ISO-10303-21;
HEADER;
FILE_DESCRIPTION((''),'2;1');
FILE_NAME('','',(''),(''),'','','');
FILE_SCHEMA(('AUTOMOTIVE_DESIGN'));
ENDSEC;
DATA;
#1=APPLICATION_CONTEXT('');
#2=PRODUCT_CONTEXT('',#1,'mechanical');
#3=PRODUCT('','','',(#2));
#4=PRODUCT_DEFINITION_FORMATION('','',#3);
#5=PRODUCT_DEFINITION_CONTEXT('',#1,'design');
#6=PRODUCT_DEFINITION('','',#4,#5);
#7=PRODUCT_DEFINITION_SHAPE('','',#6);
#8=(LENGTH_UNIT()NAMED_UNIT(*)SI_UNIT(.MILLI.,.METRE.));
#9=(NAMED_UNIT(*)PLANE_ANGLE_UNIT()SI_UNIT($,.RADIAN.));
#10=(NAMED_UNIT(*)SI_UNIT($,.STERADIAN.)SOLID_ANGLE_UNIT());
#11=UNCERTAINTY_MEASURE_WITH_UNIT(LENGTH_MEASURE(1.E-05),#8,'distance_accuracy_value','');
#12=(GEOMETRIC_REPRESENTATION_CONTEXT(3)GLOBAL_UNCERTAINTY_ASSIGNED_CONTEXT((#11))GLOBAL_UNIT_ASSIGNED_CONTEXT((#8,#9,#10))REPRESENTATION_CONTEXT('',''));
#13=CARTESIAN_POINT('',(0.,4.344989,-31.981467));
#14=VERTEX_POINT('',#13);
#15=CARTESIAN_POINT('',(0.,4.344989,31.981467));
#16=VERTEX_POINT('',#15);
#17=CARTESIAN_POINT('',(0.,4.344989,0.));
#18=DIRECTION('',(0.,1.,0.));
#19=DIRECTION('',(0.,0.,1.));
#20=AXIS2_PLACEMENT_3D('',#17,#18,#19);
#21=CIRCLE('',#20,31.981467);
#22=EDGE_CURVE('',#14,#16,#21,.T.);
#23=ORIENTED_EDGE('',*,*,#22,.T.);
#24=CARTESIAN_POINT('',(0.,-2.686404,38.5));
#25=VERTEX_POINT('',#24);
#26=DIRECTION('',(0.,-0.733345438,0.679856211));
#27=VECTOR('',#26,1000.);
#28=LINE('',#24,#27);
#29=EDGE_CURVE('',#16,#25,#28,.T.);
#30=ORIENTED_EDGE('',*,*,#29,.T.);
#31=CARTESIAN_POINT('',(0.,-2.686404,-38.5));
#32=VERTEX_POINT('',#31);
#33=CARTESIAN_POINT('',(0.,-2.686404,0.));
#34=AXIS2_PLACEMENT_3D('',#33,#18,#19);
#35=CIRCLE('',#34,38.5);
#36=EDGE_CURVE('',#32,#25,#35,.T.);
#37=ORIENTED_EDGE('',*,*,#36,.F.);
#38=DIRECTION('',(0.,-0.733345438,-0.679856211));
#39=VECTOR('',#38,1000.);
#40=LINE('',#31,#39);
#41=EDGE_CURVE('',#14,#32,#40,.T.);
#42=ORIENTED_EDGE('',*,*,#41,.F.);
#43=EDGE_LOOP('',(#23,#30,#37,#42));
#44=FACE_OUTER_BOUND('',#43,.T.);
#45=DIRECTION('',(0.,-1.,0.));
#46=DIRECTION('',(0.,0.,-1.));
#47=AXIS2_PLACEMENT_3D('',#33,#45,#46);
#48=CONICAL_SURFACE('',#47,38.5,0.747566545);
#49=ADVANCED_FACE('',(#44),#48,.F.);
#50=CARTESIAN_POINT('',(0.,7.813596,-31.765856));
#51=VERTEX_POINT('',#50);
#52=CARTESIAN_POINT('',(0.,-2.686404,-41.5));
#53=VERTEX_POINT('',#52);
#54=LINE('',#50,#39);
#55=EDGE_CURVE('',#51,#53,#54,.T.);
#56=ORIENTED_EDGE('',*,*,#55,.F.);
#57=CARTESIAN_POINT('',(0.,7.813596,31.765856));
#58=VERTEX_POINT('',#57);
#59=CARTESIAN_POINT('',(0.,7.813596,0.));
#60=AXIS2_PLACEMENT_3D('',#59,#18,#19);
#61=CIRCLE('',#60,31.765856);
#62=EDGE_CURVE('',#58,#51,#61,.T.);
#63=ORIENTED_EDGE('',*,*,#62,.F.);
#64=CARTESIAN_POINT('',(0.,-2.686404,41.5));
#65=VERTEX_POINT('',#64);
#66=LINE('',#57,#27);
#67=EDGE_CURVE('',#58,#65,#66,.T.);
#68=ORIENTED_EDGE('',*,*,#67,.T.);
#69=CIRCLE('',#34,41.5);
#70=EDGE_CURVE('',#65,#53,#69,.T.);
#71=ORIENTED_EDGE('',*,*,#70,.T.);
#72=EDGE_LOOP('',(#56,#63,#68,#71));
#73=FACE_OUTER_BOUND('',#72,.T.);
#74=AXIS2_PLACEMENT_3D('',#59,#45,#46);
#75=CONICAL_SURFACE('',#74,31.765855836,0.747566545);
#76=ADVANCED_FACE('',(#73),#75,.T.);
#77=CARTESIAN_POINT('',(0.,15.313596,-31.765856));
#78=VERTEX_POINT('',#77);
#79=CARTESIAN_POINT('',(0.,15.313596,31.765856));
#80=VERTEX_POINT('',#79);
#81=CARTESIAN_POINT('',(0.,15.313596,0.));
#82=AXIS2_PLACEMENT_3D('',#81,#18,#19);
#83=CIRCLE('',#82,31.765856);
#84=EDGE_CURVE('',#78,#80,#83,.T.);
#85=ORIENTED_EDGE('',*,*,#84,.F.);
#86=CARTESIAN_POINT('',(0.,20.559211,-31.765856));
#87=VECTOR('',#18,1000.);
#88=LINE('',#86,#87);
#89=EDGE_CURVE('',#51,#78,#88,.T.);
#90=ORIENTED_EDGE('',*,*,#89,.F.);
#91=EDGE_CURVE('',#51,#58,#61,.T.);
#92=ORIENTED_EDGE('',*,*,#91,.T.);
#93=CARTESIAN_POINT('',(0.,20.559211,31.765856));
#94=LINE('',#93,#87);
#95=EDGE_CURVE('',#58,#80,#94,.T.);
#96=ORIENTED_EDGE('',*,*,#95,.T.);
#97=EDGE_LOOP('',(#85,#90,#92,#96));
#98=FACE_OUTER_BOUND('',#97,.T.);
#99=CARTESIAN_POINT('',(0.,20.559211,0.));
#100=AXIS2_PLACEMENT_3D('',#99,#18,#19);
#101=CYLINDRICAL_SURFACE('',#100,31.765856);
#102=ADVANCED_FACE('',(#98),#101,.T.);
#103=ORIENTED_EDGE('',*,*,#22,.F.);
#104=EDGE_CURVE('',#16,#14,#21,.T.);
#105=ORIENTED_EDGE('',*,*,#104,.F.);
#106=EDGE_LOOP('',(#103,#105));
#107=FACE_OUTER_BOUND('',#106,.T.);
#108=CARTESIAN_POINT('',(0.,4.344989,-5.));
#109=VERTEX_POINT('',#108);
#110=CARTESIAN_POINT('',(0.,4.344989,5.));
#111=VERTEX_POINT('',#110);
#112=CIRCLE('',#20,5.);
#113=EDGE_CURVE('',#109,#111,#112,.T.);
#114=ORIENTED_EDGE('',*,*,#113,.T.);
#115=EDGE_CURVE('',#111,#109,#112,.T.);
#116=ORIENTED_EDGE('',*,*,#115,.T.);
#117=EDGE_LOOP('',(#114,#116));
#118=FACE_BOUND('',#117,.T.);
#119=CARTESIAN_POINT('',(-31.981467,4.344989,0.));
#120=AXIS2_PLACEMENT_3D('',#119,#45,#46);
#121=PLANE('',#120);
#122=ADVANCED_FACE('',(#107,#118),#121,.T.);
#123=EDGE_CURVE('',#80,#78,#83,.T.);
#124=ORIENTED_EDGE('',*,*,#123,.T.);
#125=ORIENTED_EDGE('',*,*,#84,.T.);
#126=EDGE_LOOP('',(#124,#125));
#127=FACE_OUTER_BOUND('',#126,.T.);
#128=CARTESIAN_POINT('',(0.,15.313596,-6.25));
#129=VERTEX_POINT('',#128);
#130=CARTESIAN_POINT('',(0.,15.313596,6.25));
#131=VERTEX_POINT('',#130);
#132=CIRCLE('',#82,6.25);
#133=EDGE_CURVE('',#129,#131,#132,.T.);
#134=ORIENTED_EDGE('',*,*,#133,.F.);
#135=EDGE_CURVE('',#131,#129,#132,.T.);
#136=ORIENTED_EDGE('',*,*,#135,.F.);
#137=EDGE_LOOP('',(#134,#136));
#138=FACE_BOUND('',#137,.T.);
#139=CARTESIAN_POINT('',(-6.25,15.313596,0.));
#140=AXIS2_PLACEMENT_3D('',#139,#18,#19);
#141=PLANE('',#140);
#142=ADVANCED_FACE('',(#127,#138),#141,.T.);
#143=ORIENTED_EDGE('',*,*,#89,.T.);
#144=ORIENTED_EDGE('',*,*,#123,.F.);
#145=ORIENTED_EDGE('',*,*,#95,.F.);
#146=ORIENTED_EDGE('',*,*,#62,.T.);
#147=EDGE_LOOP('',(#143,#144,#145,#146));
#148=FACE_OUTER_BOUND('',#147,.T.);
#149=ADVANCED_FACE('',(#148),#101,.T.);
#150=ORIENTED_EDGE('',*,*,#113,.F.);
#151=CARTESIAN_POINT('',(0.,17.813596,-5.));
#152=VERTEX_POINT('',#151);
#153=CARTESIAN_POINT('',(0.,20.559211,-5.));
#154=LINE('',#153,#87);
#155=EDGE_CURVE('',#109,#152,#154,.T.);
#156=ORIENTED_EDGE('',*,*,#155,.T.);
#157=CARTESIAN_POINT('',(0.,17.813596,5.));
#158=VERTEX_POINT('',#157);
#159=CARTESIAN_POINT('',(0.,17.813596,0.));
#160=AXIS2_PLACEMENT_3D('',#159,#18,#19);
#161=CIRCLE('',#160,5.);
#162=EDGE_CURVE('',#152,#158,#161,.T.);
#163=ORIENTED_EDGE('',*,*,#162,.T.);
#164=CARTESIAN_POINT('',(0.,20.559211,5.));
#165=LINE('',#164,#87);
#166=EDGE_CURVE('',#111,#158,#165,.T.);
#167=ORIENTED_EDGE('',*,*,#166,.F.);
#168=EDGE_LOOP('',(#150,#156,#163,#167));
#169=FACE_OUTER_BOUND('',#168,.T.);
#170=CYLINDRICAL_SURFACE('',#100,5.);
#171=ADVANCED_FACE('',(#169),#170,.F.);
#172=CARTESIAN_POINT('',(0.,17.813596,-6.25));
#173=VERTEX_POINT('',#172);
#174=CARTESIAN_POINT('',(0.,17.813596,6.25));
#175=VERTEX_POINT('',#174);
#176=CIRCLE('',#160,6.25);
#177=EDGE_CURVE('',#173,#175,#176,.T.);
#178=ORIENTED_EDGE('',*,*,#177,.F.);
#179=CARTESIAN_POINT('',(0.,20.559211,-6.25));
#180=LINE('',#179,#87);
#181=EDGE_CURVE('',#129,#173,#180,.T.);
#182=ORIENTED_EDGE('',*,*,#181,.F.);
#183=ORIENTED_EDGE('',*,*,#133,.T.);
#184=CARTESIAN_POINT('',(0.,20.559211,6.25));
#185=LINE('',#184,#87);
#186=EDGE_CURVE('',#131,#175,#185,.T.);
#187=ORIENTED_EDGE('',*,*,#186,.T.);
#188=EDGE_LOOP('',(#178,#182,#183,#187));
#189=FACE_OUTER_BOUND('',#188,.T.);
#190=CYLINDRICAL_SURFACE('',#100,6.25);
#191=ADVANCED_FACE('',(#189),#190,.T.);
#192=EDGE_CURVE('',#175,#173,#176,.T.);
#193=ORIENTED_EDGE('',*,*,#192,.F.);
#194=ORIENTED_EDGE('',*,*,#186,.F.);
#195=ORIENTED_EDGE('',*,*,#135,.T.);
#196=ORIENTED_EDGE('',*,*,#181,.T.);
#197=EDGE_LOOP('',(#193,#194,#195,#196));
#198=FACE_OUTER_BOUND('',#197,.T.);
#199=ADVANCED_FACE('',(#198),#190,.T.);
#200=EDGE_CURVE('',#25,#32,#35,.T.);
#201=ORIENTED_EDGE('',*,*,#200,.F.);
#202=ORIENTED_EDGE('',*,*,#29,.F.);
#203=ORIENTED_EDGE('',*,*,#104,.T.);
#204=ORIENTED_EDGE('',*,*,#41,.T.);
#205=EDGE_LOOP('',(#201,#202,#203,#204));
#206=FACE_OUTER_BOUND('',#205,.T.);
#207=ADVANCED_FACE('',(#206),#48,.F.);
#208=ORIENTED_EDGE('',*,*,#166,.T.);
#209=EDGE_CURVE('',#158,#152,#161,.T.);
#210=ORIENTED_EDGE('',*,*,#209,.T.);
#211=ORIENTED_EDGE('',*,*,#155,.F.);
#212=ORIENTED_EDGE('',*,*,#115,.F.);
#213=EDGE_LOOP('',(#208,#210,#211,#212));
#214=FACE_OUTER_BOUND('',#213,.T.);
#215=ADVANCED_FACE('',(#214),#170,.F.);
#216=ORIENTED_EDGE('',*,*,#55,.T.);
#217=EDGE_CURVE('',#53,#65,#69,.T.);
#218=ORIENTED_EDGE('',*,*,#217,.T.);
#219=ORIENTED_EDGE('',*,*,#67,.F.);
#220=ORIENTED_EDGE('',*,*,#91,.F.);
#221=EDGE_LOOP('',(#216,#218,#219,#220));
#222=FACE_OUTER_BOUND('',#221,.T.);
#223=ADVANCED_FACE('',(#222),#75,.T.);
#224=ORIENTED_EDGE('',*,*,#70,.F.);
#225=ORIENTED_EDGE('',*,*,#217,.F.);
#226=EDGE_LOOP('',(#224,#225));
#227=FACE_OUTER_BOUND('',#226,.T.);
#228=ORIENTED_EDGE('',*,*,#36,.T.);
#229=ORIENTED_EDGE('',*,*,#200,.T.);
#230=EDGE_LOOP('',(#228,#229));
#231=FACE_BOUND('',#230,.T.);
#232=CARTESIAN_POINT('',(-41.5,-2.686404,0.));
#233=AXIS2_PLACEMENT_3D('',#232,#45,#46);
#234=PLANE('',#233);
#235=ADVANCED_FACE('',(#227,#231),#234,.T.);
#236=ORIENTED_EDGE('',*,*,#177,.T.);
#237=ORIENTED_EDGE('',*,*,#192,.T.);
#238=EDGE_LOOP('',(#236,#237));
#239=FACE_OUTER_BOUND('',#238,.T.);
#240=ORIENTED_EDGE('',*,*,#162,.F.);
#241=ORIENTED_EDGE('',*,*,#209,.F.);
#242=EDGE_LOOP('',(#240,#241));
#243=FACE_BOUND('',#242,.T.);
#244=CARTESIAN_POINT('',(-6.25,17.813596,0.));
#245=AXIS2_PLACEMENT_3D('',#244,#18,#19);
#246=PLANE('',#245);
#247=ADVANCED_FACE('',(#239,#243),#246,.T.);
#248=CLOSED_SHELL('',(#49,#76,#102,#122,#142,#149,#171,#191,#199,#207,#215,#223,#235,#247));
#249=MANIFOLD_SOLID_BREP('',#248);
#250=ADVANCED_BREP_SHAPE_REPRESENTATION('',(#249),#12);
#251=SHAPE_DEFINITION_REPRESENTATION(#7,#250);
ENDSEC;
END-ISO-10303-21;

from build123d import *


with BuildPart() as part:
    # 草图1 → 旋转1 (revolve)
    with BuildSketch(Plane.XY, mode=Mode.PRIVATE) as revolve_1_sk:
        Polygon((-6.25, 17.813596491), (-5, 17.813596491), (-5, 4.34498949), (-31.981467322, 4.34498949), (-38.5, -2.686403509), (-41.5, -2.686403509), (-31.765855836, 7.813596491), (-31.765855836, 15.313596491), (-6.25, 15.313596491), align=None)
    revolve(revolve_1_sk.sketch.rotate(Axis((0, 20.559210526, 0), (0, -1, 0)), 270), axis=Axis((0, 20.559210526, 0), (0, -1, 0)))


solid = part.part
